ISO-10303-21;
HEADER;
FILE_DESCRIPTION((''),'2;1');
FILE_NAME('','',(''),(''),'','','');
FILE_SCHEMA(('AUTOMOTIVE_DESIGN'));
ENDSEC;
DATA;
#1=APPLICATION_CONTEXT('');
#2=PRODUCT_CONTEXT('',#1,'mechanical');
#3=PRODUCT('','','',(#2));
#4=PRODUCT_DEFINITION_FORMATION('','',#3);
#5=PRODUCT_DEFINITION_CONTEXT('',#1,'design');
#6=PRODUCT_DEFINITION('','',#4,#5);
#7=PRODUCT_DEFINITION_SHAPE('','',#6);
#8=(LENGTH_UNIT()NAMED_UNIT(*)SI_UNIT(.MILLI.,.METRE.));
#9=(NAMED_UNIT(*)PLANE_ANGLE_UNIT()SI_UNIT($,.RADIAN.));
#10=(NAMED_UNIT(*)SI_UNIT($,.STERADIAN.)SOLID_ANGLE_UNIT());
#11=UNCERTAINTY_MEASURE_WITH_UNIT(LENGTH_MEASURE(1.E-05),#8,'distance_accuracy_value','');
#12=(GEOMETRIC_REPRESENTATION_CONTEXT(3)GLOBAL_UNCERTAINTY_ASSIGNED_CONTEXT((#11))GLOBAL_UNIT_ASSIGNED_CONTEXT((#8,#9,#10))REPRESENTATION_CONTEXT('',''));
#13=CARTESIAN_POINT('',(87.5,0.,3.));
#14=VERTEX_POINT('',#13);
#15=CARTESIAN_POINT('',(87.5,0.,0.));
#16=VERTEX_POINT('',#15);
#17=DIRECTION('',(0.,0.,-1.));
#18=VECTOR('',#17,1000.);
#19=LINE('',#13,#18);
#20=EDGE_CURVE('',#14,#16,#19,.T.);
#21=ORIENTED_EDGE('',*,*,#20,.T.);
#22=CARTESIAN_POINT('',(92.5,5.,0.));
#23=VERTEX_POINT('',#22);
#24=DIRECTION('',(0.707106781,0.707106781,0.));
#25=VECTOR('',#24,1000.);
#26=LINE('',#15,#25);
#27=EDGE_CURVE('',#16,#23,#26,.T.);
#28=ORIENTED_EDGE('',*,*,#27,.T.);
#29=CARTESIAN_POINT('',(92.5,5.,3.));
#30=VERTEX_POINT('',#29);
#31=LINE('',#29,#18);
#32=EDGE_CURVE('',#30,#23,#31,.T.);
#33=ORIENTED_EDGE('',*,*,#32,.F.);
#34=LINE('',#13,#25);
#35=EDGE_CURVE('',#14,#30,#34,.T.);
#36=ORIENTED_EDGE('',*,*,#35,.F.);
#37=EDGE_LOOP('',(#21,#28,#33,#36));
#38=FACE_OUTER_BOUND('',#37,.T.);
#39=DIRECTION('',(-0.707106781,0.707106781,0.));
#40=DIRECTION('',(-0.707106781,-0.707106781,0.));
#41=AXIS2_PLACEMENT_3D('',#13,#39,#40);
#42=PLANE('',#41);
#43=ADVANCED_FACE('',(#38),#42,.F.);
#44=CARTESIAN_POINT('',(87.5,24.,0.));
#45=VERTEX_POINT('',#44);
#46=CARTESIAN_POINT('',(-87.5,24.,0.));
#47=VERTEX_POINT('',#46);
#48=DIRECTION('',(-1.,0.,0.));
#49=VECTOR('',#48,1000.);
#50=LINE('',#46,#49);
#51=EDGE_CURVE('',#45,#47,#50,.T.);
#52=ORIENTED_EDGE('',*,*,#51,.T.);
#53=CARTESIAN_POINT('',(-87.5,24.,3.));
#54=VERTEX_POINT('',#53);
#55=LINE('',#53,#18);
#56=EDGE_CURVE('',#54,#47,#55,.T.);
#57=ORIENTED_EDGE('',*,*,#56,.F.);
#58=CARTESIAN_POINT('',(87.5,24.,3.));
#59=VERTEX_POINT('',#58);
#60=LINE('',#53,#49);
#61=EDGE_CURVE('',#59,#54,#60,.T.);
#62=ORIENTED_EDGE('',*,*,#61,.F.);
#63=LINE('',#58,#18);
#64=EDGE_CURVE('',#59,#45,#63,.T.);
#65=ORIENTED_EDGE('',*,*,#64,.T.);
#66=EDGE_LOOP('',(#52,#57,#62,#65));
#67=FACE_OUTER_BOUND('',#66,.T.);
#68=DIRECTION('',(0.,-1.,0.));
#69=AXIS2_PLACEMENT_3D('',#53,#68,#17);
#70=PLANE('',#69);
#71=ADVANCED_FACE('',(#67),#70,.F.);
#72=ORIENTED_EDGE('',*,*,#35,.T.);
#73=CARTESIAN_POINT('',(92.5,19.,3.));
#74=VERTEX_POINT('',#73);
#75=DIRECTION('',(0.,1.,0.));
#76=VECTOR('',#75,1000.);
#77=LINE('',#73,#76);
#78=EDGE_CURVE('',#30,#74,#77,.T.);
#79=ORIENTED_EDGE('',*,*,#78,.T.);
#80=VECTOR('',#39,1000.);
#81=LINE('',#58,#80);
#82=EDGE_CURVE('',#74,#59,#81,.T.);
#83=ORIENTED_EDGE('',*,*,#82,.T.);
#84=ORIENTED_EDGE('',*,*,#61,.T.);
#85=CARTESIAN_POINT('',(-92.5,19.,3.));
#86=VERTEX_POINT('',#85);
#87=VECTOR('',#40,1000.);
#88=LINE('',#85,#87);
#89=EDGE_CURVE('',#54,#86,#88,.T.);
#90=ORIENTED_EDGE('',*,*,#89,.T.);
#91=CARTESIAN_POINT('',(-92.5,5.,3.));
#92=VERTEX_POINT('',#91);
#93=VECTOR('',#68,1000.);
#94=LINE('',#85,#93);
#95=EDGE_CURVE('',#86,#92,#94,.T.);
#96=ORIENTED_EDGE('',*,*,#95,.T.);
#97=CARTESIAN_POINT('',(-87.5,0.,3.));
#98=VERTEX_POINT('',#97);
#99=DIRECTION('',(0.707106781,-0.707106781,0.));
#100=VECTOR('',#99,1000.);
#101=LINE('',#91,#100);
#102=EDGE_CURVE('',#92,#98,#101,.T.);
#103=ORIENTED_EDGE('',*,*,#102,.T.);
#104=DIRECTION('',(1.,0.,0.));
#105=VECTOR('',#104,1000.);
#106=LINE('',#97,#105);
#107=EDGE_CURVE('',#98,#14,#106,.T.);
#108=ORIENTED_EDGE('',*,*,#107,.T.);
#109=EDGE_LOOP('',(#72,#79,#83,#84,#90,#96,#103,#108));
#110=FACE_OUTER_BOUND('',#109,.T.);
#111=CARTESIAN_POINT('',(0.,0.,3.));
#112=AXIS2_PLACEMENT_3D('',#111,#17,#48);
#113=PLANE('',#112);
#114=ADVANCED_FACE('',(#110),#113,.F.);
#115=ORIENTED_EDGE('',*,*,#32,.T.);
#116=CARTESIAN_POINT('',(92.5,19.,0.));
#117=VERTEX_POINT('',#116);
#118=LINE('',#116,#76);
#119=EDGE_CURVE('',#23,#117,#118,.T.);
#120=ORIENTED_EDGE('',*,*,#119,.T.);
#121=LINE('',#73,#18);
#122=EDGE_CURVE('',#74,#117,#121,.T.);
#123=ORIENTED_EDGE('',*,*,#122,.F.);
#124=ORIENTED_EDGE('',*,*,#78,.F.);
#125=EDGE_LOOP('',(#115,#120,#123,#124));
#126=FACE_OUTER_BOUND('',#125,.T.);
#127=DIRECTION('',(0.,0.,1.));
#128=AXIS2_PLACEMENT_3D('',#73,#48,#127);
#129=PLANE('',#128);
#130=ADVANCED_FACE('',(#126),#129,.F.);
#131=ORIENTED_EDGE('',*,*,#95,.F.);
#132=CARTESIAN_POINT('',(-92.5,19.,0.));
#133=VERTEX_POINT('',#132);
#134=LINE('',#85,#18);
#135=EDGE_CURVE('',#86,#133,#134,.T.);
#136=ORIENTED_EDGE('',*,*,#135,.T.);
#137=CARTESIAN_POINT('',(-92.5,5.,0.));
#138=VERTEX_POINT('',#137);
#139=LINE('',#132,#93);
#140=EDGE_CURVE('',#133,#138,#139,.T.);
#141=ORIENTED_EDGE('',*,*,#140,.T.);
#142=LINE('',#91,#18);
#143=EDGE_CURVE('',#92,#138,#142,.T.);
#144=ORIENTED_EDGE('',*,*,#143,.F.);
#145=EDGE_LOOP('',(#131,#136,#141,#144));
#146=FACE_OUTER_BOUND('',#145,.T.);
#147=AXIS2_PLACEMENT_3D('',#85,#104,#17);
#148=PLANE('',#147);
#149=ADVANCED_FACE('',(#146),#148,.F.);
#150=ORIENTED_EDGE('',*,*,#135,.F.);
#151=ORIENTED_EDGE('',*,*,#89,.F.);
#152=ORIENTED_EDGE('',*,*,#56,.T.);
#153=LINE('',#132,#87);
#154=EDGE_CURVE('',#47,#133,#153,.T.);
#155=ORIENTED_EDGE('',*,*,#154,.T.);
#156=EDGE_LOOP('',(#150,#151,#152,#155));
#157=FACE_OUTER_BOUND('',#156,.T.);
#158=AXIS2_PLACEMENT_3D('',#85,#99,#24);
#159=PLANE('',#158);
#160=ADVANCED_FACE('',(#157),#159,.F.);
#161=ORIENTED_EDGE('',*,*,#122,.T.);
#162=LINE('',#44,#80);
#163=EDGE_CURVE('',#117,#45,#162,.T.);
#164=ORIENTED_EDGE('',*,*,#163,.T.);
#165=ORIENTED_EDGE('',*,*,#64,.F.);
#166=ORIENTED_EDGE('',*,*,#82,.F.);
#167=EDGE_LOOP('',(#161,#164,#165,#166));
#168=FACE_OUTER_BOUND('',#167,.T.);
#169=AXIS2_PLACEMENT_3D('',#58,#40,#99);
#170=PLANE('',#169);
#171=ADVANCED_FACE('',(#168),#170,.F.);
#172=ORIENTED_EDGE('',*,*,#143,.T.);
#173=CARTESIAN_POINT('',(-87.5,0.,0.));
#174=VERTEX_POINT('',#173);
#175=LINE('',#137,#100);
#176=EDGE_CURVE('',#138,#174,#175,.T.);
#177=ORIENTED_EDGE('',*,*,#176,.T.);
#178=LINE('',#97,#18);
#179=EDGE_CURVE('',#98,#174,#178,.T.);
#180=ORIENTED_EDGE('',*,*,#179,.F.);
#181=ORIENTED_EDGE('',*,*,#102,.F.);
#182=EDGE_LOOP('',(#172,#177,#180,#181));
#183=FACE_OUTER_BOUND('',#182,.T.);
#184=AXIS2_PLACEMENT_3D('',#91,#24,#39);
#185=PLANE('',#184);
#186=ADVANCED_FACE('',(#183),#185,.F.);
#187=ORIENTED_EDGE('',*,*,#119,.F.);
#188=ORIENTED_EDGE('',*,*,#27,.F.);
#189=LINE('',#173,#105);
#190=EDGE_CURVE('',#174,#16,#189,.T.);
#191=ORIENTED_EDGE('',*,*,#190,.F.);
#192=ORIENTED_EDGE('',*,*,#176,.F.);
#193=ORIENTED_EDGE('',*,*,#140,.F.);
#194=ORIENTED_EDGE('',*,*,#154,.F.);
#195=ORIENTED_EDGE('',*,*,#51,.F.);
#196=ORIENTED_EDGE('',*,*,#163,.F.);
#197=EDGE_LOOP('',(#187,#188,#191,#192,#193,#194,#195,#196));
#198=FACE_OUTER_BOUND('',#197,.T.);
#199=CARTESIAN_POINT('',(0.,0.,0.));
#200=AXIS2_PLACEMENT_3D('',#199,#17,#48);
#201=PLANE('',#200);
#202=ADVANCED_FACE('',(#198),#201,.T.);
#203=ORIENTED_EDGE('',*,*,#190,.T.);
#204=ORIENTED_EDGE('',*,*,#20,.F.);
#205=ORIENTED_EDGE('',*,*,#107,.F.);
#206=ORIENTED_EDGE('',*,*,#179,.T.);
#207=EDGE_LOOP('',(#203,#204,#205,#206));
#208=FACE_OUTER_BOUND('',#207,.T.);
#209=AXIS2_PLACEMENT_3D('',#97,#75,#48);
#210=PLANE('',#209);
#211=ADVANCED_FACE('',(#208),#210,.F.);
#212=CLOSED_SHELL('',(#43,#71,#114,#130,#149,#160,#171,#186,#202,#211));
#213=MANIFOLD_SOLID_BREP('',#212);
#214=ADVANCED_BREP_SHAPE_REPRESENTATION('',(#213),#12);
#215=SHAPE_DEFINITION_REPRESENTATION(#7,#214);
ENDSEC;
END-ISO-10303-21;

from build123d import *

# Parameters (mm, degrees)
EXTRUDE_1_DEPTH = 3


with BuildPart() as part:
    # 草图1 → 凸台-拉伸1 (new body)
    with BuildSketch(Plane.XY):
        Polygon((-92.5, 19), (-87.5, 24), (87.5, 24), (92.5, 19), (92.5, 5), (87.5, 0), (-87.5, 0), (-92.5, 5), align=None)
    extrude(amount=EXTRUDE_1_DEPTH)


solid = part.part
